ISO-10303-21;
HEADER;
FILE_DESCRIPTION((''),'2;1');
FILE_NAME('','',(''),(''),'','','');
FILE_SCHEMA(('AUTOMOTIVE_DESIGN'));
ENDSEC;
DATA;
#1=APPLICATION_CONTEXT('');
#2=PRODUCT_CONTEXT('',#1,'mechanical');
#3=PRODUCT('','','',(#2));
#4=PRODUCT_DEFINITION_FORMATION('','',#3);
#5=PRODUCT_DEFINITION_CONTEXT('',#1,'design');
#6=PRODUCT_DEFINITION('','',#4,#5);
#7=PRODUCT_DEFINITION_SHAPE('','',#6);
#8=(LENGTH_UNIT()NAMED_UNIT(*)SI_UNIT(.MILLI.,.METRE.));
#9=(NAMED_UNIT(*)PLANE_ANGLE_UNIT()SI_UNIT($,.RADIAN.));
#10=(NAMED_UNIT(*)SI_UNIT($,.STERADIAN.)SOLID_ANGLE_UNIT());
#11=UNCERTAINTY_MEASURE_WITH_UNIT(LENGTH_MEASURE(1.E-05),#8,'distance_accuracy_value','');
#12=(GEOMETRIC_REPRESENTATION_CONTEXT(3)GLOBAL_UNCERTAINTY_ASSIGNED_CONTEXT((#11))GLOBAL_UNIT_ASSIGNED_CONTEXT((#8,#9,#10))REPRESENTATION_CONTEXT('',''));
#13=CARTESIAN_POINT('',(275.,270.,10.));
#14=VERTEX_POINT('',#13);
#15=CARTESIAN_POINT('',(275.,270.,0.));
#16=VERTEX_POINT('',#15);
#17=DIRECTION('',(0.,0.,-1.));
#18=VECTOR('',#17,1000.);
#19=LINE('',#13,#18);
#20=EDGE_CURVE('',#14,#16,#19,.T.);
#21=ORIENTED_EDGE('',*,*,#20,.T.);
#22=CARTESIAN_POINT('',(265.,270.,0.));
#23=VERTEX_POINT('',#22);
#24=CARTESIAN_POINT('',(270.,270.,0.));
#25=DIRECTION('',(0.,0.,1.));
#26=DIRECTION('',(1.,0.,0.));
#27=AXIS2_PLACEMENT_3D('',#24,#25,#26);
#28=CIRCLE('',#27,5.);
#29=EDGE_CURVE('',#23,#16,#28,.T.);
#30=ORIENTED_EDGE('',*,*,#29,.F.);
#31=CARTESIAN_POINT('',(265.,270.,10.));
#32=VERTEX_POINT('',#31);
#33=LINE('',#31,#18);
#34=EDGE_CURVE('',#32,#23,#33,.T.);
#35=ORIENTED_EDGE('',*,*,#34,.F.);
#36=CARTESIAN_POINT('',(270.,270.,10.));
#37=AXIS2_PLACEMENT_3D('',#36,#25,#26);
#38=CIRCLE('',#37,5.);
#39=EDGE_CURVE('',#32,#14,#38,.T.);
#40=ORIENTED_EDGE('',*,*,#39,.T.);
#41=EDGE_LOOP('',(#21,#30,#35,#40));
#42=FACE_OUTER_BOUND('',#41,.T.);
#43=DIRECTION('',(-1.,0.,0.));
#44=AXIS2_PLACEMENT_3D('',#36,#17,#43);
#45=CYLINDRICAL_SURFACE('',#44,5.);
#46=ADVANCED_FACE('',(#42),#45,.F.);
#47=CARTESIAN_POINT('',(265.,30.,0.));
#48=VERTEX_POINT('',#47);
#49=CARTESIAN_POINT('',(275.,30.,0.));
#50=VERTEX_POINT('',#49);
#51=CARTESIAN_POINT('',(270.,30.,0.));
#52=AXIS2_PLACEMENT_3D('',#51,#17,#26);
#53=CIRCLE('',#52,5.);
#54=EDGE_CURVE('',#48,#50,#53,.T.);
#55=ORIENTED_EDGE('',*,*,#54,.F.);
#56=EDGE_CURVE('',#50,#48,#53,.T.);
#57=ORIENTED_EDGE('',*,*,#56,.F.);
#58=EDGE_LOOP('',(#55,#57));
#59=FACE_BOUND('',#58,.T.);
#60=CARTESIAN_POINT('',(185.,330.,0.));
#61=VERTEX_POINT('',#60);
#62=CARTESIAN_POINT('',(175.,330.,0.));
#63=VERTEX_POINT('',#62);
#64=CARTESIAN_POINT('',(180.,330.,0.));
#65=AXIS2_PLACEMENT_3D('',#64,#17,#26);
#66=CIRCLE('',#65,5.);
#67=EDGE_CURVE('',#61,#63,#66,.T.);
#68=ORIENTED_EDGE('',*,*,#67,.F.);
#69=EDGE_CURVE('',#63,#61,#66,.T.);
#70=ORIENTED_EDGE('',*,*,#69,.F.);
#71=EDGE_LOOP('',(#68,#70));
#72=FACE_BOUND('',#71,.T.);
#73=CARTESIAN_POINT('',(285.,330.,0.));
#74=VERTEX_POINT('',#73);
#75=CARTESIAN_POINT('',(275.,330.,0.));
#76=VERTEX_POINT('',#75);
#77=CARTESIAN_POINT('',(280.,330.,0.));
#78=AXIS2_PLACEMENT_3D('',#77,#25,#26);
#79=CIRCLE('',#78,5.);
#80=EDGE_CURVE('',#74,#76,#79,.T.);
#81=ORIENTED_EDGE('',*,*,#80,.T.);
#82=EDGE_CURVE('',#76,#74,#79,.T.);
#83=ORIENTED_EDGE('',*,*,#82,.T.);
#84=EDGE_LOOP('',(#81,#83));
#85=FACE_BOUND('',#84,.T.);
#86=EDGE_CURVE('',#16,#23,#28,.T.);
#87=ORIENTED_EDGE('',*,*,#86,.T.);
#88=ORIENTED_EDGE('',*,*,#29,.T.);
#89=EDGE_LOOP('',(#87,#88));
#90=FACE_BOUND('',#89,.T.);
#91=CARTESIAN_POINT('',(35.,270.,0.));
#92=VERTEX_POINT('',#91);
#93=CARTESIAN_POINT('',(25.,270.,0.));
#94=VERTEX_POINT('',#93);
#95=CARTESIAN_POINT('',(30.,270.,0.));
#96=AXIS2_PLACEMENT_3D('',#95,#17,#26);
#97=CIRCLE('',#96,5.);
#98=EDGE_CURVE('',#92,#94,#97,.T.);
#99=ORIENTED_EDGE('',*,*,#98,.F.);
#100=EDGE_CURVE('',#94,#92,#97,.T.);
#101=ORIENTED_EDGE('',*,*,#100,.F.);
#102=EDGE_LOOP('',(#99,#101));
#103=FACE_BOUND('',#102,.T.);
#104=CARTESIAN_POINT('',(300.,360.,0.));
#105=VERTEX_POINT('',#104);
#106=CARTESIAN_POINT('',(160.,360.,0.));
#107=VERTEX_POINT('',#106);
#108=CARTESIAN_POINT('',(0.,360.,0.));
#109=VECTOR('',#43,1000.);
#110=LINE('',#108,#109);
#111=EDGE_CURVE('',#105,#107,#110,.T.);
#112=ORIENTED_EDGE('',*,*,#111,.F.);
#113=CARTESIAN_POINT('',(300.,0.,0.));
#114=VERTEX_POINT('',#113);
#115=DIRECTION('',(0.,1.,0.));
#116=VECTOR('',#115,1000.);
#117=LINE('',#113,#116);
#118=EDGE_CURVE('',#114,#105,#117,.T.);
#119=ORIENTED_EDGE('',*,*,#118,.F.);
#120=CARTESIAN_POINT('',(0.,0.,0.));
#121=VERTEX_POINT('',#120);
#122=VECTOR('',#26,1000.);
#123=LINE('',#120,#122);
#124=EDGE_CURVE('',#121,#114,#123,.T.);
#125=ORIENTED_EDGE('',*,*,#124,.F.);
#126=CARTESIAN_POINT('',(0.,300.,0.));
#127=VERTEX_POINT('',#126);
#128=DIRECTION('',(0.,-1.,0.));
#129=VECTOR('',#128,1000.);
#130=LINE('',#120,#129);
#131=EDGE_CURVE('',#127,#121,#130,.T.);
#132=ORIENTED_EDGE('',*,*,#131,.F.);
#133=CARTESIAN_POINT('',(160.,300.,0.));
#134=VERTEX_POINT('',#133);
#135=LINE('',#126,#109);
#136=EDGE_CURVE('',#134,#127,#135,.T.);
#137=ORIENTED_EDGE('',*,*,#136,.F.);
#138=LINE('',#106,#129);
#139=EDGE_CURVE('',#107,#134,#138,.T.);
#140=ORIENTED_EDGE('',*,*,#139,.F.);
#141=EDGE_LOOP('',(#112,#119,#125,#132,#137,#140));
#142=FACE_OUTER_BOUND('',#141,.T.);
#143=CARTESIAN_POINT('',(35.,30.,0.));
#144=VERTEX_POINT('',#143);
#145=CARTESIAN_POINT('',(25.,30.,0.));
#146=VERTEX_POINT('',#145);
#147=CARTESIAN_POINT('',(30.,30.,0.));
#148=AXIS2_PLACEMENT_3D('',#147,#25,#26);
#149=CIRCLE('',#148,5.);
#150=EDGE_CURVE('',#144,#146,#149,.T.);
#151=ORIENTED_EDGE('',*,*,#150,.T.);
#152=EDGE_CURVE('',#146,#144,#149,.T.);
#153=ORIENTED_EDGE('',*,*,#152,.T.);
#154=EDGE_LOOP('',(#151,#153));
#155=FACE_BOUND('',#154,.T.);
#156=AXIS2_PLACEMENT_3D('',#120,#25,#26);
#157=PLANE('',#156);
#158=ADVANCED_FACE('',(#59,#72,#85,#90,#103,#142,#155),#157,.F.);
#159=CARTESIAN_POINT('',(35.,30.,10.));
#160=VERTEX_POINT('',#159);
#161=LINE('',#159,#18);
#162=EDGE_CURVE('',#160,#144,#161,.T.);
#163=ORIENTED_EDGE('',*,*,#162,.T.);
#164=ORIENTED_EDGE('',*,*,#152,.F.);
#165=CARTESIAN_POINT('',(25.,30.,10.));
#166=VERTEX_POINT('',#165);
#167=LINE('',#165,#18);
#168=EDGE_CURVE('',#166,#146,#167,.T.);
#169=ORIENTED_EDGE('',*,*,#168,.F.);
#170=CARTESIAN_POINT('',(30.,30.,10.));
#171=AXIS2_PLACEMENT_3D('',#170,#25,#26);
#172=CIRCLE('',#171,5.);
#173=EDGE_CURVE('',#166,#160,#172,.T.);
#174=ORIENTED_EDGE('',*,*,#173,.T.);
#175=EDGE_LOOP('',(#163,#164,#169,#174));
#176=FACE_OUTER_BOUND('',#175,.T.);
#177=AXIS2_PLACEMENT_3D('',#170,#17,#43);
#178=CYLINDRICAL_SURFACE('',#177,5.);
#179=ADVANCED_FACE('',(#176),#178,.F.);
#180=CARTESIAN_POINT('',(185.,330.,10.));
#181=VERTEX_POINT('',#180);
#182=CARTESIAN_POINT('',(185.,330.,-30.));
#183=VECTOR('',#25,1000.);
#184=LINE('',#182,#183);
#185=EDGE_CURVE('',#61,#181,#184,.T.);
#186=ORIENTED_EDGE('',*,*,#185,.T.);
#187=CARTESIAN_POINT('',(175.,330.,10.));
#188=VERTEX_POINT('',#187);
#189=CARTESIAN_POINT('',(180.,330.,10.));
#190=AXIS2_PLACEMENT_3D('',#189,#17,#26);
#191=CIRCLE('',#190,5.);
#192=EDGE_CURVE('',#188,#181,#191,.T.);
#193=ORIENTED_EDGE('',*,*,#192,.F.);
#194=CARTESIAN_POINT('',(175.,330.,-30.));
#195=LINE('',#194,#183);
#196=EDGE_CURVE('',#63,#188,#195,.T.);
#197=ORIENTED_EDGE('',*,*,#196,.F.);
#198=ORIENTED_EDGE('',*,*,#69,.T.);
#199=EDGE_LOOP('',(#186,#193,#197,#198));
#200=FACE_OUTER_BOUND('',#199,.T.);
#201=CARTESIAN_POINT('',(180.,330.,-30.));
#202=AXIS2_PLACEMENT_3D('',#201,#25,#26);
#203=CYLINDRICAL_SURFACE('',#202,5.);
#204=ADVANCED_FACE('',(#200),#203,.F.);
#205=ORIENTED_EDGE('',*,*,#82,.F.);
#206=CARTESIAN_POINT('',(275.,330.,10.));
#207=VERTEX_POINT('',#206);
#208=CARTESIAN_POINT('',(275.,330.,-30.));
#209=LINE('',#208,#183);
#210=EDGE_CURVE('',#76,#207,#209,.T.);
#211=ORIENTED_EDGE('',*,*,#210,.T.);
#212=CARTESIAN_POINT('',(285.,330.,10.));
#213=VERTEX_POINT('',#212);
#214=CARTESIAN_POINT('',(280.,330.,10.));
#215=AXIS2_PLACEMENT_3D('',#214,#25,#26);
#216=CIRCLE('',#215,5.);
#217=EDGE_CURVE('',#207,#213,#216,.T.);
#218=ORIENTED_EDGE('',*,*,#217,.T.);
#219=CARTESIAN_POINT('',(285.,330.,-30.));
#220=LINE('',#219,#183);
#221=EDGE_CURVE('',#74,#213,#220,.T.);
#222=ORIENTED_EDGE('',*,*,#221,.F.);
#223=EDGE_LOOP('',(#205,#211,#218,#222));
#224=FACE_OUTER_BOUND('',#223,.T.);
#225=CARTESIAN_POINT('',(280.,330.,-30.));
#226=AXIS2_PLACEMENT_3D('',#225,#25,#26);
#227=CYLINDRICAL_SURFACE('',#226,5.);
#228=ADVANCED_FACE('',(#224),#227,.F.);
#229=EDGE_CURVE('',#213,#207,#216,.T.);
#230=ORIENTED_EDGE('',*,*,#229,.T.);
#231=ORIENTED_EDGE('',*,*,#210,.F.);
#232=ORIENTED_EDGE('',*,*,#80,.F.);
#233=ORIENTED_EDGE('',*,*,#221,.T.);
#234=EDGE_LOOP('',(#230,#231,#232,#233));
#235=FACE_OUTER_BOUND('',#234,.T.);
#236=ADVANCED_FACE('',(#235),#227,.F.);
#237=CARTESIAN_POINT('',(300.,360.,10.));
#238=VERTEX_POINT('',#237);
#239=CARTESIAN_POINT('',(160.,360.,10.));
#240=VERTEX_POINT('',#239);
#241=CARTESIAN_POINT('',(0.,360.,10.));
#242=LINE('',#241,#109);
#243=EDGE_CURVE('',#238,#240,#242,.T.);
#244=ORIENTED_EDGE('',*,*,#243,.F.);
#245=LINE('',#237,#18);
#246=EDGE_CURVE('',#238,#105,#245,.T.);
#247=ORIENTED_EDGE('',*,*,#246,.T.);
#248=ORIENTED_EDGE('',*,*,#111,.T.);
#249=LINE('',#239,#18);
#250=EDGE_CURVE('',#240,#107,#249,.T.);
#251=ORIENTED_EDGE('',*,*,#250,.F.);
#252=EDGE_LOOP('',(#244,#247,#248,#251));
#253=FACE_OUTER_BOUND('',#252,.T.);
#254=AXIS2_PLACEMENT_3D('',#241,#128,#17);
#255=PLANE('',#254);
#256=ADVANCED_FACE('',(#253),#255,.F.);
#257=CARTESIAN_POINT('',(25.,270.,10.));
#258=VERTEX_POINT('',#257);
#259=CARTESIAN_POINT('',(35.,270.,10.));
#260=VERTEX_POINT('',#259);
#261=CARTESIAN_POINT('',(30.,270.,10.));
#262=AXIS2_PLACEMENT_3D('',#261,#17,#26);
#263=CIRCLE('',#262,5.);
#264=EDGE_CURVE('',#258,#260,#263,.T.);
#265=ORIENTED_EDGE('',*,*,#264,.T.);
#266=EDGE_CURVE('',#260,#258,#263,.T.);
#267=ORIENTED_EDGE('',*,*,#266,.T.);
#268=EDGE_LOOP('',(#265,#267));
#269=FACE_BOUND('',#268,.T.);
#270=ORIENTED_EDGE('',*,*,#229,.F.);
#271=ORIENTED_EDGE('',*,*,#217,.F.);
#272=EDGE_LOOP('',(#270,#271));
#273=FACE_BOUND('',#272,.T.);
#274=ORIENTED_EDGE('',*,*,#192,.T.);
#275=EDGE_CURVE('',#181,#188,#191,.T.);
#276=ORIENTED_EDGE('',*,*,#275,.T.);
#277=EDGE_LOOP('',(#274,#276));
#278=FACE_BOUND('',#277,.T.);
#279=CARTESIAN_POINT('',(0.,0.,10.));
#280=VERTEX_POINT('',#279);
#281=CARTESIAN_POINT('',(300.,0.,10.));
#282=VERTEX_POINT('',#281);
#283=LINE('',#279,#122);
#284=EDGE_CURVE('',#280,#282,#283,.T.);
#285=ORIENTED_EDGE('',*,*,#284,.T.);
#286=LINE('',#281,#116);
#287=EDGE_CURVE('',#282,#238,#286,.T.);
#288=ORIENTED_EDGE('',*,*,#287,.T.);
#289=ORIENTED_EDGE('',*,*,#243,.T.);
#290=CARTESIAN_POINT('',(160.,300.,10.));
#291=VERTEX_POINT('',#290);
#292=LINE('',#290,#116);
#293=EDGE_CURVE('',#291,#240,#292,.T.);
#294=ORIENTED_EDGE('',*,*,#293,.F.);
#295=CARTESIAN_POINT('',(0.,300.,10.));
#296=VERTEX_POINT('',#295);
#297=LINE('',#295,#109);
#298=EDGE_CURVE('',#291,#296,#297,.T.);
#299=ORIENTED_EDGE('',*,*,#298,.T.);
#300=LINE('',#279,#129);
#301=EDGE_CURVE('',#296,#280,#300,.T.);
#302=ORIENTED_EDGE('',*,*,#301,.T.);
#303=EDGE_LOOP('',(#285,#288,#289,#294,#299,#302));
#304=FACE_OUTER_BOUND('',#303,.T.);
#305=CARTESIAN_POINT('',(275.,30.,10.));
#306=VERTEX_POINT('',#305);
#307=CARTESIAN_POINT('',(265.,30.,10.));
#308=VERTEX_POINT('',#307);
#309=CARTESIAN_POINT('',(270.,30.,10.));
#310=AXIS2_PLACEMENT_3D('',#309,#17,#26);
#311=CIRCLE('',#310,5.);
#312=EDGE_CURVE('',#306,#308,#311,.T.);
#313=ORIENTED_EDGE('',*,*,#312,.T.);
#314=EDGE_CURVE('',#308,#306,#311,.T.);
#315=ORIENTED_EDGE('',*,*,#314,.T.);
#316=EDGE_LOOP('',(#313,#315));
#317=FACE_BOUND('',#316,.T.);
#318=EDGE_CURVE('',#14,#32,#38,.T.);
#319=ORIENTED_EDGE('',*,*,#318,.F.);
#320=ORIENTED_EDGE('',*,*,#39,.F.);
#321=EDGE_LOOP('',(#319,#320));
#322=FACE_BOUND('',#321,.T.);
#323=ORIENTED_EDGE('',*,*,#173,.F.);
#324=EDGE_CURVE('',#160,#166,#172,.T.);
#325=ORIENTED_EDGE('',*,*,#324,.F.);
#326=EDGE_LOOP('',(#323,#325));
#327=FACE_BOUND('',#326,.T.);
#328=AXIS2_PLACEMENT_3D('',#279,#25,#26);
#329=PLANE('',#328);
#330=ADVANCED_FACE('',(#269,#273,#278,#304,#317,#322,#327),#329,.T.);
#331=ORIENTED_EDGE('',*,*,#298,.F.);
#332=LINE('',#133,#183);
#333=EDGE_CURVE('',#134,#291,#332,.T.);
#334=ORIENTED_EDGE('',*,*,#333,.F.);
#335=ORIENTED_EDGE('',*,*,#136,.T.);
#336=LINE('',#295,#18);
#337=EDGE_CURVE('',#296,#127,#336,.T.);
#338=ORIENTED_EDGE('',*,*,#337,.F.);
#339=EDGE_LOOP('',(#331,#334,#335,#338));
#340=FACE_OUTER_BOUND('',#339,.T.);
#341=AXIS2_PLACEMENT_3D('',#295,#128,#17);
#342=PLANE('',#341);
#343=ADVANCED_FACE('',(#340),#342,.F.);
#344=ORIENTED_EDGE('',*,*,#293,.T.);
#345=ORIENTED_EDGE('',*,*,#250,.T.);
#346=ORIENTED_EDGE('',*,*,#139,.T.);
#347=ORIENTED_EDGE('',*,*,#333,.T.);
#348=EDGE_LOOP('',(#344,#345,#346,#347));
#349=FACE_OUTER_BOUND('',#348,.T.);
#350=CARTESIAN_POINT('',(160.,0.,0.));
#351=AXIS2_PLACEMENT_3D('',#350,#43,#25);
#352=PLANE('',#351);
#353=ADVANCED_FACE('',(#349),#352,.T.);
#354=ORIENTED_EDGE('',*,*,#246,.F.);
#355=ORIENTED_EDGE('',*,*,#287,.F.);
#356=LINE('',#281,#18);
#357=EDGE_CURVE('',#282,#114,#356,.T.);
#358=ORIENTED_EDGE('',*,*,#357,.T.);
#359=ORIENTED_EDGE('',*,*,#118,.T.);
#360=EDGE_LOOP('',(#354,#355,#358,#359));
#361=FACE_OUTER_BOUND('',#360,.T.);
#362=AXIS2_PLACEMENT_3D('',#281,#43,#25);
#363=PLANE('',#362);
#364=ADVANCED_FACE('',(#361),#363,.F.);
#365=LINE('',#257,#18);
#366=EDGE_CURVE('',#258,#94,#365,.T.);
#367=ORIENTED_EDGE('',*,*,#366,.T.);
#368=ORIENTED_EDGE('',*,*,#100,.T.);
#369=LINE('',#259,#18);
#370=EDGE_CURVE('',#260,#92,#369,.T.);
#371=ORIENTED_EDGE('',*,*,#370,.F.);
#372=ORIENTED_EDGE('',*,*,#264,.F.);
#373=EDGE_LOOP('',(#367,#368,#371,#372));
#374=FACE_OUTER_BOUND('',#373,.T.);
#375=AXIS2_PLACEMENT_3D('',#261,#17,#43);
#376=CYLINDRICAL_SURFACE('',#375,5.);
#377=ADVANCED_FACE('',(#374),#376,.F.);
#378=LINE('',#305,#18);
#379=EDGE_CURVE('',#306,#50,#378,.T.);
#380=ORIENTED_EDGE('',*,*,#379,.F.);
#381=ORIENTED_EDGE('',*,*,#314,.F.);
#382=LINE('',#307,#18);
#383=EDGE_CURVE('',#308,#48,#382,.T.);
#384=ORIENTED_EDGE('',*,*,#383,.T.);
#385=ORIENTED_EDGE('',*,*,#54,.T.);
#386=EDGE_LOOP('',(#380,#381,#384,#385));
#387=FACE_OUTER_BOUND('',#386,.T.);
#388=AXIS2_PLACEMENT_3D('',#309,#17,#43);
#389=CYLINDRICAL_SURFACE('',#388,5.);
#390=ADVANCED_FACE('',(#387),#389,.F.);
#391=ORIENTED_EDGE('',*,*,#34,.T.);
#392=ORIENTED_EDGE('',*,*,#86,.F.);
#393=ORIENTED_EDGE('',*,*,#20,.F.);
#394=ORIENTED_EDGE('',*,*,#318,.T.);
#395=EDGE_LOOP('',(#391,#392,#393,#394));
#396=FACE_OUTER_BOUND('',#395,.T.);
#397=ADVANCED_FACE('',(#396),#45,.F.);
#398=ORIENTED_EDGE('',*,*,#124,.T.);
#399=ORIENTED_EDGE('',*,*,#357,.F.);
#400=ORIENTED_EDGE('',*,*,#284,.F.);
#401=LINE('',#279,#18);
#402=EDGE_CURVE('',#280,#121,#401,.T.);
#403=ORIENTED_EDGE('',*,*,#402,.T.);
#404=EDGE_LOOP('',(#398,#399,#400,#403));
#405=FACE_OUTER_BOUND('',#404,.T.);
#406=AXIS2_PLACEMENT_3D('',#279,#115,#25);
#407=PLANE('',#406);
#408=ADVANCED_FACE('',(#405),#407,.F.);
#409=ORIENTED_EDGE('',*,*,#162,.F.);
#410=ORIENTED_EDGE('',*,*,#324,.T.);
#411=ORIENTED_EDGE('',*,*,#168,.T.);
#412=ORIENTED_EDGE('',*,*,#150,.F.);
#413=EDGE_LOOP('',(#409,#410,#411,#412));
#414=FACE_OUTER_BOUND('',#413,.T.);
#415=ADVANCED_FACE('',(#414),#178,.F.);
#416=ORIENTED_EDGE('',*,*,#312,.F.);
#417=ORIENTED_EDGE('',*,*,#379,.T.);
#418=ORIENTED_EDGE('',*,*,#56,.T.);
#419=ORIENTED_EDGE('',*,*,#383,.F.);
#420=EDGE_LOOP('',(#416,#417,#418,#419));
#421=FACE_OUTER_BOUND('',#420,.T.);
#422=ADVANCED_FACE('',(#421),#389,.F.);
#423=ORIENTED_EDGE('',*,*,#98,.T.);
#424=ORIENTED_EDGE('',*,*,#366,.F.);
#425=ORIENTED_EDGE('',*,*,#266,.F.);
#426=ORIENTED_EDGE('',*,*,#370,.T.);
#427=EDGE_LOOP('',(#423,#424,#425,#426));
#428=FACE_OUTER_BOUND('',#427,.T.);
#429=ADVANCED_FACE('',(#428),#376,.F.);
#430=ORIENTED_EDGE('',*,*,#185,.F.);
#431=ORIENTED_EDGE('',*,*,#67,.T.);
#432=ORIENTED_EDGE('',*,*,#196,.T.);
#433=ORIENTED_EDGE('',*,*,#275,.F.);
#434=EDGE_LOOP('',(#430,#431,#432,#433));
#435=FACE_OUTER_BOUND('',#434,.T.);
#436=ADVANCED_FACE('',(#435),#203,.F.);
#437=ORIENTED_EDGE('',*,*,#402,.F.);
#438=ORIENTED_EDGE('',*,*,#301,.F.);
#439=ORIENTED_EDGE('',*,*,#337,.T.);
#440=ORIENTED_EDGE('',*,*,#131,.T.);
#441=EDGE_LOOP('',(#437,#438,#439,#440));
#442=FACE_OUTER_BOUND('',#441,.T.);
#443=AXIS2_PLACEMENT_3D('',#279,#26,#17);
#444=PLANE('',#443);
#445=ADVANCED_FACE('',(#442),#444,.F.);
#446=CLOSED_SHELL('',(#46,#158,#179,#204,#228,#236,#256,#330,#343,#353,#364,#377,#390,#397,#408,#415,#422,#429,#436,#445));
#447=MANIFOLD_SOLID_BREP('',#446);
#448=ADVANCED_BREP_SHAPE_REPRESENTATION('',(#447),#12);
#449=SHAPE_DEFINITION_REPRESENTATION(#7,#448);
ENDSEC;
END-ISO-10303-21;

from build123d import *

# Parameters (mm, degrees)
SKETCH_1_R          = 5
EXTRUDE_1_DEPTH     = 10
SKETCH_3_W          = 10
SKETCH_3_H          = 60
EXTRUDE_2_DEPTH     = 40
CUT_EXTRUDE_2_DEPTH = 40


with BuildPart() as part:
    # 草图1 → 凸台-拉伸1 (new body)
    with BuildSketch(Plane.XY):
        Polygon((300, 360), (200, 360), (200, 300), (0, 300), (0, 0), (300, 0), (300, 300), align=None)
        with Locations((270, 30)):
            Circle(SKETCH_1_R, mode=Mode.SUBTRACT)
        with Locations((30, 30)):
            Circle(SKETCH_1_R, mode=Mode.SUBTRACT)
        with Locations((270, 270)):
            Circle(SKETCH_1_R, mode=Mode.SUBTRACT)
        with Locations((30, 270)):
            Circle(SKETCH_1_R, mode=Mode.SUBTRACT)
    extrude(amount=EXTRUDE_1_DEPTH)

    # 草图3 → 凸台-拉伸2 (add)
    with BuildSketch(Plane.ZY.offset(-200)):
        with Locations((5, 330)):
            Rectangle(SKETCH_3_W, SKETCH_3_H)
    extrude(amount=EXTRUDE_2_DEPTH)

    # 草图4 → 切除-拉伸2 (cut)
    with BuildSketch(Plane.XY.offset(10)):
        with BuildLine():
            ThreePointArc((175, 330), (180, 325), (185, 330))
            Line((185, 330), (175, 330))
        make_face()
        with BuildLine():
            Line((175, 330), (185, 330))
            ThreePointArc((185, 330), (180, 335), (175, 330))
        make_face()
        with BuildLine():
            ThreePointArc((285, 330), (280, 335), (275, 330))
            Line((275, 330), (280, 330))
            Line((280, 330), (285, 330))
        make_face()
        with BuildLine():
            Line((280, 330), (275, 330))
            ThreePointArc((275, 330), (280, 325), (285, 330))
            Line((285, 330), (280, 330))
        make_face()
    extrude(amount=-CUT_EXTRUDE_2_DEPTH, mode=Mode.SUBTRACT)


solid = part.part
